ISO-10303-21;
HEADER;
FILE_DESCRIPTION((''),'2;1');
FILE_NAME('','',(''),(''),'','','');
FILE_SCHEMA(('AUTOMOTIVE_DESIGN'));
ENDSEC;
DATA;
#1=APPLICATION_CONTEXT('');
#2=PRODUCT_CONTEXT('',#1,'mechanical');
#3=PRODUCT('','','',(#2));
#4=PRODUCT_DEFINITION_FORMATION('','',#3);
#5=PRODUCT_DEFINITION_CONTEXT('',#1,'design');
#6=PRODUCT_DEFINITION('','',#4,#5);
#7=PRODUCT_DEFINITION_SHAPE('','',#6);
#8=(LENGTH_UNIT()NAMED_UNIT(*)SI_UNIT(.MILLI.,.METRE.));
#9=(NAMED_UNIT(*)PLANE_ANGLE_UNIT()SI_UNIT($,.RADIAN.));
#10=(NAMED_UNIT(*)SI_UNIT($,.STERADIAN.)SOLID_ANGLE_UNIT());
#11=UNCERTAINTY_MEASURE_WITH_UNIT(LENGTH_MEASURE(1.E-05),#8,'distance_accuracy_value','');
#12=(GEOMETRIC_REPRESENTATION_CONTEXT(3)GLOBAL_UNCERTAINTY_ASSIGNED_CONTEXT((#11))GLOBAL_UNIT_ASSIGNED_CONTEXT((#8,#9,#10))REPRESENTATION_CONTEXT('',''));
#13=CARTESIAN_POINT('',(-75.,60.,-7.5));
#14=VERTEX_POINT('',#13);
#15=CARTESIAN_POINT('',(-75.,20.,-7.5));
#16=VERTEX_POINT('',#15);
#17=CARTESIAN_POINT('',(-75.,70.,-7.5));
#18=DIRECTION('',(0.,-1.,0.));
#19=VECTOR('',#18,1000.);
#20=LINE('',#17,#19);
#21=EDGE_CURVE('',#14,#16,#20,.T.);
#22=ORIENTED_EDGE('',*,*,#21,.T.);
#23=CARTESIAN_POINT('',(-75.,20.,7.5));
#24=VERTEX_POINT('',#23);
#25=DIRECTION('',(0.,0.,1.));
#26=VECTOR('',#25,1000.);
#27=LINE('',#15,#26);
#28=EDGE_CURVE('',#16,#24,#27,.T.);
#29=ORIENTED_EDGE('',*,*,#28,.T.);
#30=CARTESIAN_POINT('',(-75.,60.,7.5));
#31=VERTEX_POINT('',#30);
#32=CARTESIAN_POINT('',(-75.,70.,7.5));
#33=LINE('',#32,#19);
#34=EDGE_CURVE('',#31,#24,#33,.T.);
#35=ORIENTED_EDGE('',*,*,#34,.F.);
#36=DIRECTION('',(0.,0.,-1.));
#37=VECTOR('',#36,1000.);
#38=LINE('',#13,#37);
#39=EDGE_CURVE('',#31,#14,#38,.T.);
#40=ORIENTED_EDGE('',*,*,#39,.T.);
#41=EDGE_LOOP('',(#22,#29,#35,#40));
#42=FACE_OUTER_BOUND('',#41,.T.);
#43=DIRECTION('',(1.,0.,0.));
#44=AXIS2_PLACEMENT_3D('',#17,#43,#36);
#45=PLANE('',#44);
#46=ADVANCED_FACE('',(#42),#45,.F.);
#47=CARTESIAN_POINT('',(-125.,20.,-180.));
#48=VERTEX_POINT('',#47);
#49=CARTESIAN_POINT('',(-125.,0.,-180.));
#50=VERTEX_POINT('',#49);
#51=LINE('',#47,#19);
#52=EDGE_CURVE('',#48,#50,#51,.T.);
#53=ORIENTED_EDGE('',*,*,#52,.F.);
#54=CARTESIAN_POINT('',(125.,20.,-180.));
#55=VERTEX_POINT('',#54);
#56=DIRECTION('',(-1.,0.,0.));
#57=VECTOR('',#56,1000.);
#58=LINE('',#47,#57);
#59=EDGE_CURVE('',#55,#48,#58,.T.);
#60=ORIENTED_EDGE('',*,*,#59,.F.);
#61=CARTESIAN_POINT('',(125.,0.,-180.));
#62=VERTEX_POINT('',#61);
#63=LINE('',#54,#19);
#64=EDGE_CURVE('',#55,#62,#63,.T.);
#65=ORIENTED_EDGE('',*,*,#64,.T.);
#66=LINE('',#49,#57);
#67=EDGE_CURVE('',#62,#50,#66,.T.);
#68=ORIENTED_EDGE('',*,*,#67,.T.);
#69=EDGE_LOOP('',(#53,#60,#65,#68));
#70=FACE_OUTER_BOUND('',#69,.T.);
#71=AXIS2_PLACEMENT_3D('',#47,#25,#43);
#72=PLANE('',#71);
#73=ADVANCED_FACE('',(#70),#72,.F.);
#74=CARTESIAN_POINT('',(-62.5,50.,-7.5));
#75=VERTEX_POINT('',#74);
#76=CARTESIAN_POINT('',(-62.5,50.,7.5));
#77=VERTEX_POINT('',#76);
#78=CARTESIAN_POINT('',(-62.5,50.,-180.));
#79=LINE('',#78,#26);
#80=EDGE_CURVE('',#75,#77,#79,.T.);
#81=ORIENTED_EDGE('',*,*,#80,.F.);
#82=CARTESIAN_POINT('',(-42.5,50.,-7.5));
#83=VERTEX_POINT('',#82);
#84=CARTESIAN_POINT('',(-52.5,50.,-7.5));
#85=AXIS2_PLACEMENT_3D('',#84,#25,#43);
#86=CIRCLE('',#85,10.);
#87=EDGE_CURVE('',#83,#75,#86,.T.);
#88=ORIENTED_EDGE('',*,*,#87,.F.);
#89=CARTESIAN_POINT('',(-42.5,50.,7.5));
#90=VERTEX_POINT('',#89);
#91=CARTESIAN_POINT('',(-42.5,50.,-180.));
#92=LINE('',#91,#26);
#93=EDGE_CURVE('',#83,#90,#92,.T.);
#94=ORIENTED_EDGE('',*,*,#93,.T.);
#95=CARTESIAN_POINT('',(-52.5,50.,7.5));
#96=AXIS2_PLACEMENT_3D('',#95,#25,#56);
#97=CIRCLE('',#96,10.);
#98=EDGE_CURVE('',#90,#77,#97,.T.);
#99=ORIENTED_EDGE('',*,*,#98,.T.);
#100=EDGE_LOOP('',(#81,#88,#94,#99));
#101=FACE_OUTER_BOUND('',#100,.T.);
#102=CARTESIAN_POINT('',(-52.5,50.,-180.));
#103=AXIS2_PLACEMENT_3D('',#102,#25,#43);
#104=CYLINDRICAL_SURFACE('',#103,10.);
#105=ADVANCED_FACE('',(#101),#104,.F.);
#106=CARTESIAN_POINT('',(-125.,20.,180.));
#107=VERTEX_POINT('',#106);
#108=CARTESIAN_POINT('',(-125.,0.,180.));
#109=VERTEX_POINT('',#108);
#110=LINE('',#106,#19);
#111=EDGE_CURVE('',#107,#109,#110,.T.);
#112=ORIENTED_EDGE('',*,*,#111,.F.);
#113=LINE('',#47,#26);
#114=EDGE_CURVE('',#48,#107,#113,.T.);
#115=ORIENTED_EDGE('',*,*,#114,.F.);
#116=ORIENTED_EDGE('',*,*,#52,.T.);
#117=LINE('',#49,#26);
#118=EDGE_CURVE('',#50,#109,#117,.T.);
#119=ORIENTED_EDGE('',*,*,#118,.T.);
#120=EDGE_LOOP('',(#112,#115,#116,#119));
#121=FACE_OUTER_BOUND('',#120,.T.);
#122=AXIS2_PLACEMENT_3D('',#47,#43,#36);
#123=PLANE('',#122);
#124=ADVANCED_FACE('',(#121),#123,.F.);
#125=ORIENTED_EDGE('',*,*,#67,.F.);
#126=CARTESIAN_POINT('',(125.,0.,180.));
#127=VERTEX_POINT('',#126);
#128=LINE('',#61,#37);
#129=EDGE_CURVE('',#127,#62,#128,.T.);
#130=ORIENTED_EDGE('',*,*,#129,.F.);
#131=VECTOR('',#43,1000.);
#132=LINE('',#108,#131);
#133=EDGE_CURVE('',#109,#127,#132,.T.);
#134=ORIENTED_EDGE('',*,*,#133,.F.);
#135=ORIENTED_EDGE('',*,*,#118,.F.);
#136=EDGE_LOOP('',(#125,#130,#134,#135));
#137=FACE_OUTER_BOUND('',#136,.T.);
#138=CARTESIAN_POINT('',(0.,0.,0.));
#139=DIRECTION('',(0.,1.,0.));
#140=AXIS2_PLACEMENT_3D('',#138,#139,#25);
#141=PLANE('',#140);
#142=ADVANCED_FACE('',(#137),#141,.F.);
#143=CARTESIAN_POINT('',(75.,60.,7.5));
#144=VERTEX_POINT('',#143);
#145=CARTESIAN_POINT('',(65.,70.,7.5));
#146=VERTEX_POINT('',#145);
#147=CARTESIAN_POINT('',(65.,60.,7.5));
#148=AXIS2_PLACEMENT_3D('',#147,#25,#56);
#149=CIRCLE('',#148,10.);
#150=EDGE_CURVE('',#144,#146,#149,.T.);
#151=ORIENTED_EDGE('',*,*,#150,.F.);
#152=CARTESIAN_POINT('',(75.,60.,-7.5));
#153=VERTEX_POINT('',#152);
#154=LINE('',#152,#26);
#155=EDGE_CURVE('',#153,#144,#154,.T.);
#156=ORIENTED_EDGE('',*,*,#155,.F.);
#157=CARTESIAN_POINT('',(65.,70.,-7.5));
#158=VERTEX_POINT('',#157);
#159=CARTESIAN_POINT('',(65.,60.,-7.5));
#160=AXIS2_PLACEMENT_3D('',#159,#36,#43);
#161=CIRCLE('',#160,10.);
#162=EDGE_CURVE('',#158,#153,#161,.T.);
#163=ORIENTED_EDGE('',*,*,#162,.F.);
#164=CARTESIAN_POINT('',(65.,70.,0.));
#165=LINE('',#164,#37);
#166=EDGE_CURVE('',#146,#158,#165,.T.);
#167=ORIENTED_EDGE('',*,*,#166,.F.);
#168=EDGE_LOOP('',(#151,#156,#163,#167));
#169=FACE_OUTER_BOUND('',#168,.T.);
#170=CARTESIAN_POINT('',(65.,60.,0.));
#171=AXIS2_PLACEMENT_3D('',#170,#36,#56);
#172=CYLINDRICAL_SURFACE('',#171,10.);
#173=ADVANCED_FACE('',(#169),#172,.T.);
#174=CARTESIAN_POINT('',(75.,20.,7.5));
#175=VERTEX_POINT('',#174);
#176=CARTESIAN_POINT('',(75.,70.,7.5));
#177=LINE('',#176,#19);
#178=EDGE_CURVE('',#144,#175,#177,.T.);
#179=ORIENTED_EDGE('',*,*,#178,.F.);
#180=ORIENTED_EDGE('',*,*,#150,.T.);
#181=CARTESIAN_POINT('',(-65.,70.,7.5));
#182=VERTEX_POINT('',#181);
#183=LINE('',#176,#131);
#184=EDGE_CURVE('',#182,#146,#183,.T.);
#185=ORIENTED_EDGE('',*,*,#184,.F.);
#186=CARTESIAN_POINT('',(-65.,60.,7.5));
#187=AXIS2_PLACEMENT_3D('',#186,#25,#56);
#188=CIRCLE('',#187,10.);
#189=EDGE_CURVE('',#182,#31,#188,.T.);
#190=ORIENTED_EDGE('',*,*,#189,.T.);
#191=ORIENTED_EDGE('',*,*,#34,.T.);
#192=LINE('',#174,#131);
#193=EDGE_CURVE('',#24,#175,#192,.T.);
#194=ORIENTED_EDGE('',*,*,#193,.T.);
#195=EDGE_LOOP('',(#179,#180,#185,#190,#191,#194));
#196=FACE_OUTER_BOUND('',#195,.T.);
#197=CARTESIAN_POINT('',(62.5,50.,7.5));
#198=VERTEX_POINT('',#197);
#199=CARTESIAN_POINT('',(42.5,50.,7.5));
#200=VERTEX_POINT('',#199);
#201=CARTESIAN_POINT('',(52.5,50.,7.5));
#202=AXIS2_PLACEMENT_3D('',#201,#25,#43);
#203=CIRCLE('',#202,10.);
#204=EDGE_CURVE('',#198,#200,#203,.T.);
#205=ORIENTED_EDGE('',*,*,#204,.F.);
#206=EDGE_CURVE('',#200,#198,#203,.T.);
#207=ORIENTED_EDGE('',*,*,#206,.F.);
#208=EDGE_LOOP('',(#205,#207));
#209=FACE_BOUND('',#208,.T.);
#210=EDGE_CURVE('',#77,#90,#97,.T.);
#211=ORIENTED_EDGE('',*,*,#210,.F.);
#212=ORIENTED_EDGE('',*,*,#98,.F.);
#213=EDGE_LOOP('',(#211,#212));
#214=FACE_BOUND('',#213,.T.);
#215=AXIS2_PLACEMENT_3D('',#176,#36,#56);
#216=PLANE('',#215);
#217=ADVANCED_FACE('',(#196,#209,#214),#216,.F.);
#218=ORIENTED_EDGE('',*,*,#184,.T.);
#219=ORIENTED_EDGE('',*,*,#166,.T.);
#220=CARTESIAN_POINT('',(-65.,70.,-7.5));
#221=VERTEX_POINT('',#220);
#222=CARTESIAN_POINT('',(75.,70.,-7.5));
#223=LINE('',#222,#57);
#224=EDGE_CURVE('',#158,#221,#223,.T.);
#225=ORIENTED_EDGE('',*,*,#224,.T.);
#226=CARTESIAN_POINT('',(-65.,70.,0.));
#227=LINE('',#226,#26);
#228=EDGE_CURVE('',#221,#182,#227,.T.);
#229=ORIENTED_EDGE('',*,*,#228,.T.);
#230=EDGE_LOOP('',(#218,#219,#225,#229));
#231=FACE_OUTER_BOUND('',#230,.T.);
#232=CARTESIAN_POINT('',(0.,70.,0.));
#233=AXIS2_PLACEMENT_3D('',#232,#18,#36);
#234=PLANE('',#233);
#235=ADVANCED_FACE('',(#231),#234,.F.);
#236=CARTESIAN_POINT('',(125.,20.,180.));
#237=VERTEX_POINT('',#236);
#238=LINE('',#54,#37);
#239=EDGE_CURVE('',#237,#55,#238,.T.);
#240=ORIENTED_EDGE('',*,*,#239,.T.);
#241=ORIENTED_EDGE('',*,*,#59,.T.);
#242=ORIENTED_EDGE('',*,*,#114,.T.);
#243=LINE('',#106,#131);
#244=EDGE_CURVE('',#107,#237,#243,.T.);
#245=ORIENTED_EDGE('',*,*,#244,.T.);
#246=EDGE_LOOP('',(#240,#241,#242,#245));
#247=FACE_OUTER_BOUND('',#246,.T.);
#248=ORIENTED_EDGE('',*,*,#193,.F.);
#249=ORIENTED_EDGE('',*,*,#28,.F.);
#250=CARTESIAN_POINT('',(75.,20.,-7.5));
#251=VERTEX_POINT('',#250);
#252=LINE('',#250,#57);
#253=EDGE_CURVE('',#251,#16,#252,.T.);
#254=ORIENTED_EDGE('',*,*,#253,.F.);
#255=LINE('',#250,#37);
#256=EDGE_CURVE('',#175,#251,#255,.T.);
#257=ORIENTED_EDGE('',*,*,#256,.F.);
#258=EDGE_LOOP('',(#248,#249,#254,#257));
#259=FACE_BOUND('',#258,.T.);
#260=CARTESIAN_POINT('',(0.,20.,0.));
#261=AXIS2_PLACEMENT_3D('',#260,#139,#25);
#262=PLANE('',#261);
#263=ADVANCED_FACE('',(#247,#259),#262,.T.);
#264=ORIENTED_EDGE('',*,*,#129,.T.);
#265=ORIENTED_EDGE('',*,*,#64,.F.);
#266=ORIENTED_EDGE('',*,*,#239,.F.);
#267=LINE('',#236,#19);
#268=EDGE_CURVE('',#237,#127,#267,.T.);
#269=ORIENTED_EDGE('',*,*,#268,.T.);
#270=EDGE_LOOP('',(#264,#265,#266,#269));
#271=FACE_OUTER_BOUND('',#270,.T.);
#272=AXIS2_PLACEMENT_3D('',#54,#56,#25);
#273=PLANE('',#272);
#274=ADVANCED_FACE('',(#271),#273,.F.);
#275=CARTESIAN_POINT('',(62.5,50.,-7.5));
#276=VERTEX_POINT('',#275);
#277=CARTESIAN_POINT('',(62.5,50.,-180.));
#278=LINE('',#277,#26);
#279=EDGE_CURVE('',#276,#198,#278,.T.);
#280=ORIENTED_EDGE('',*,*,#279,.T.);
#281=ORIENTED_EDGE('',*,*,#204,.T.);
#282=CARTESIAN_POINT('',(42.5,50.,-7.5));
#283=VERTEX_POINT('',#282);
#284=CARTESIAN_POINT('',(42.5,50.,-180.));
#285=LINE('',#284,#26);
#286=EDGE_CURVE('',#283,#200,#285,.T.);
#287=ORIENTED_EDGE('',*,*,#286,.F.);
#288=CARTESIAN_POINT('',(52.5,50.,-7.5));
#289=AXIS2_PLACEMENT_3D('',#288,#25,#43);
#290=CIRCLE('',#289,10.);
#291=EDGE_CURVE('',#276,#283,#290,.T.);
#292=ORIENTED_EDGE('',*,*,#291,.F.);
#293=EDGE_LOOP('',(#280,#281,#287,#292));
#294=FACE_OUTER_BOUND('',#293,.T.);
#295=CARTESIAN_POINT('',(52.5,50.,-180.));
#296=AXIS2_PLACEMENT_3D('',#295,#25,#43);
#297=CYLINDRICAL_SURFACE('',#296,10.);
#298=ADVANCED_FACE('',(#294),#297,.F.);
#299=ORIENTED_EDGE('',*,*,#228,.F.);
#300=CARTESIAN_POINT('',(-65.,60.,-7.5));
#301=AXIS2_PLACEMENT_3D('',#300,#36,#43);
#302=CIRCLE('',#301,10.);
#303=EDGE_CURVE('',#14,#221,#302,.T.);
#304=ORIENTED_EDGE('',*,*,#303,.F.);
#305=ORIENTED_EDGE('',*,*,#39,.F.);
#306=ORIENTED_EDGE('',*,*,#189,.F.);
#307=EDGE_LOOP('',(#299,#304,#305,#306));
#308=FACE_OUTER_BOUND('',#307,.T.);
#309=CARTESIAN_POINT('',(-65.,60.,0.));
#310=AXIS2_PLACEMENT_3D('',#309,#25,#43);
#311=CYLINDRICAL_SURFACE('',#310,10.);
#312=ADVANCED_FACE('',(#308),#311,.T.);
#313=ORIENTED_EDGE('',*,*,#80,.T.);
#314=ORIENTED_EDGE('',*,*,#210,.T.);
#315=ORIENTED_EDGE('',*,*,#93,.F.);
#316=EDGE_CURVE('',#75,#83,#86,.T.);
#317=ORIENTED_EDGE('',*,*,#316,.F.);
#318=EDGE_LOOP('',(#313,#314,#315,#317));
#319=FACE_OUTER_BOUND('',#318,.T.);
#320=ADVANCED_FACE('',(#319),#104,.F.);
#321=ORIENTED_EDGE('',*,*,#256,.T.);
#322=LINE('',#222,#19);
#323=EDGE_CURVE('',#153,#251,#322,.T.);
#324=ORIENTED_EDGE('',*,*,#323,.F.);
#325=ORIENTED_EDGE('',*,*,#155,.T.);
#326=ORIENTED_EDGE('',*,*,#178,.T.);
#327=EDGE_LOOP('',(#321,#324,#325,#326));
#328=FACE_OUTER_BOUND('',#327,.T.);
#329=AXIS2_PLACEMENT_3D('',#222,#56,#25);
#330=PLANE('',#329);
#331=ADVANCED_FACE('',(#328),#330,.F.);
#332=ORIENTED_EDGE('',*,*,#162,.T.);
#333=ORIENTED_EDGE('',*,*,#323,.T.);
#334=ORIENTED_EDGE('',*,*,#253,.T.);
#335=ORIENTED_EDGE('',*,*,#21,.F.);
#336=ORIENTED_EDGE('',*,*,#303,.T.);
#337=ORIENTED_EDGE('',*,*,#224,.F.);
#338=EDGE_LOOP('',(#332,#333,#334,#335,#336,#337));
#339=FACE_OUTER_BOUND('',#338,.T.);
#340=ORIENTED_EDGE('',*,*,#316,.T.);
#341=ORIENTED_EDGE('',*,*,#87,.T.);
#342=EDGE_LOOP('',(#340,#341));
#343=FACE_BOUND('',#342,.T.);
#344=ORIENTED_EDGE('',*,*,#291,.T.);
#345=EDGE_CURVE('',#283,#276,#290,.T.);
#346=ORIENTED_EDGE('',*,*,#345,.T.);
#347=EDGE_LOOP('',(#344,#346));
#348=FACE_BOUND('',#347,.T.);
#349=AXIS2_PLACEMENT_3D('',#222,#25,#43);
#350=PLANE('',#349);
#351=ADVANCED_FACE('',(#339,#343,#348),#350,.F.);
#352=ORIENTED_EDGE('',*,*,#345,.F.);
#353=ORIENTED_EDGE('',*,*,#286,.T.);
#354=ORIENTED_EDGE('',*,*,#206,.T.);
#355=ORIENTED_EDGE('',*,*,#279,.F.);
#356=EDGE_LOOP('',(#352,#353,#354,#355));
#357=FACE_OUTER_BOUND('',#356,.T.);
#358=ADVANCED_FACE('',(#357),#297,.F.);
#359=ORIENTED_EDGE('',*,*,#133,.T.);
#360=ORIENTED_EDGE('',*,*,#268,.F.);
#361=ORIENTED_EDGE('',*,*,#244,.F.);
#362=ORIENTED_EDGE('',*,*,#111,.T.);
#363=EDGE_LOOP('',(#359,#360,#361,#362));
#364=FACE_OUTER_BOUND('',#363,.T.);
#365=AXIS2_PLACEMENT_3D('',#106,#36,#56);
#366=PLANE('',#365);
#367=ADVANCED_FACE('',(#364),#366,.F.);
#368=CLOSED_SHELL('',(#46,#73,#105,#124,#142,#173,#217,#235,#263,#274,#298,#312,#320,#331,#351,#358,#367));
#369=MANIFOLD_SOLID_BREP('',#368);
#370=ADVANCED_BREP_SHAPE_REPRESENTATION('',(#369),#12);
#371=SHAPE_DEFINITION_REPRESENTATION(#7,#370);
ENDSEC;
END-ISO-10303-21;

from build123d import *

# Parameters (mm, degrees)
SKETCH1_W           = 250
SKETCH1_H           = 360
BOSS_EXTRUDE1_DEPTH = 20
SKETCH2_W           = 150
SKETCH2_H           = 15
BOSS_EXTRUDE2_DEPTH = 50
FILLET1_R           = 10
SKETCH3_R           = 10
CUT_EXTRUDE1_DEPTH  = 236.968747931


with BuildPart() as part:
    # Sketch1 → Boss-Extrude1 (new body)
    with BuildSketch(Plane(origin=(0, 0, 0), x_dir=(1, 0, 0), z_dir=(0, 1, 0))):
        Rectangle(SKETCH1_W, SKETCH1_H)
    extrude(amount=BOSS_EXTRUDE1_DEPTH)

    # Sketch2 → Boss-Extrude2 (add)
    with BuildSketch(Plane(origin=(0, 20, 0), x_dir=(1, 0, 0), z_dir=(0, 1, 0))):
        Rectangle(SKETCH2_W, SKETCH2_H)
    extrude(amount=BOSS_EXTRUDE2_DEPTH)

    # Fillet1
    fillet1_edges = [part.edges().sort_by_distance(p)[0] for p in [
        (-75, 70, 0),
        (75, 70, 0),
    ]]
    fillet(fillet1_edges, radius=FILLET1_R)

    # Sketch3 → Cut-Extrude1 (cut, through all)
    with BuildSketch(Plane.XY.offset(7.5)):
        with Locations((52.5, 50)):
            Circle(SKETCH3_R)
        with Locations((-52.5, 50)):
            Circle(SKETCH3_R)
    extrude(amount=-CUT_EXTRUDE1_DEPTH, mode=Mode.SUBTRACT)


solid = part.part
